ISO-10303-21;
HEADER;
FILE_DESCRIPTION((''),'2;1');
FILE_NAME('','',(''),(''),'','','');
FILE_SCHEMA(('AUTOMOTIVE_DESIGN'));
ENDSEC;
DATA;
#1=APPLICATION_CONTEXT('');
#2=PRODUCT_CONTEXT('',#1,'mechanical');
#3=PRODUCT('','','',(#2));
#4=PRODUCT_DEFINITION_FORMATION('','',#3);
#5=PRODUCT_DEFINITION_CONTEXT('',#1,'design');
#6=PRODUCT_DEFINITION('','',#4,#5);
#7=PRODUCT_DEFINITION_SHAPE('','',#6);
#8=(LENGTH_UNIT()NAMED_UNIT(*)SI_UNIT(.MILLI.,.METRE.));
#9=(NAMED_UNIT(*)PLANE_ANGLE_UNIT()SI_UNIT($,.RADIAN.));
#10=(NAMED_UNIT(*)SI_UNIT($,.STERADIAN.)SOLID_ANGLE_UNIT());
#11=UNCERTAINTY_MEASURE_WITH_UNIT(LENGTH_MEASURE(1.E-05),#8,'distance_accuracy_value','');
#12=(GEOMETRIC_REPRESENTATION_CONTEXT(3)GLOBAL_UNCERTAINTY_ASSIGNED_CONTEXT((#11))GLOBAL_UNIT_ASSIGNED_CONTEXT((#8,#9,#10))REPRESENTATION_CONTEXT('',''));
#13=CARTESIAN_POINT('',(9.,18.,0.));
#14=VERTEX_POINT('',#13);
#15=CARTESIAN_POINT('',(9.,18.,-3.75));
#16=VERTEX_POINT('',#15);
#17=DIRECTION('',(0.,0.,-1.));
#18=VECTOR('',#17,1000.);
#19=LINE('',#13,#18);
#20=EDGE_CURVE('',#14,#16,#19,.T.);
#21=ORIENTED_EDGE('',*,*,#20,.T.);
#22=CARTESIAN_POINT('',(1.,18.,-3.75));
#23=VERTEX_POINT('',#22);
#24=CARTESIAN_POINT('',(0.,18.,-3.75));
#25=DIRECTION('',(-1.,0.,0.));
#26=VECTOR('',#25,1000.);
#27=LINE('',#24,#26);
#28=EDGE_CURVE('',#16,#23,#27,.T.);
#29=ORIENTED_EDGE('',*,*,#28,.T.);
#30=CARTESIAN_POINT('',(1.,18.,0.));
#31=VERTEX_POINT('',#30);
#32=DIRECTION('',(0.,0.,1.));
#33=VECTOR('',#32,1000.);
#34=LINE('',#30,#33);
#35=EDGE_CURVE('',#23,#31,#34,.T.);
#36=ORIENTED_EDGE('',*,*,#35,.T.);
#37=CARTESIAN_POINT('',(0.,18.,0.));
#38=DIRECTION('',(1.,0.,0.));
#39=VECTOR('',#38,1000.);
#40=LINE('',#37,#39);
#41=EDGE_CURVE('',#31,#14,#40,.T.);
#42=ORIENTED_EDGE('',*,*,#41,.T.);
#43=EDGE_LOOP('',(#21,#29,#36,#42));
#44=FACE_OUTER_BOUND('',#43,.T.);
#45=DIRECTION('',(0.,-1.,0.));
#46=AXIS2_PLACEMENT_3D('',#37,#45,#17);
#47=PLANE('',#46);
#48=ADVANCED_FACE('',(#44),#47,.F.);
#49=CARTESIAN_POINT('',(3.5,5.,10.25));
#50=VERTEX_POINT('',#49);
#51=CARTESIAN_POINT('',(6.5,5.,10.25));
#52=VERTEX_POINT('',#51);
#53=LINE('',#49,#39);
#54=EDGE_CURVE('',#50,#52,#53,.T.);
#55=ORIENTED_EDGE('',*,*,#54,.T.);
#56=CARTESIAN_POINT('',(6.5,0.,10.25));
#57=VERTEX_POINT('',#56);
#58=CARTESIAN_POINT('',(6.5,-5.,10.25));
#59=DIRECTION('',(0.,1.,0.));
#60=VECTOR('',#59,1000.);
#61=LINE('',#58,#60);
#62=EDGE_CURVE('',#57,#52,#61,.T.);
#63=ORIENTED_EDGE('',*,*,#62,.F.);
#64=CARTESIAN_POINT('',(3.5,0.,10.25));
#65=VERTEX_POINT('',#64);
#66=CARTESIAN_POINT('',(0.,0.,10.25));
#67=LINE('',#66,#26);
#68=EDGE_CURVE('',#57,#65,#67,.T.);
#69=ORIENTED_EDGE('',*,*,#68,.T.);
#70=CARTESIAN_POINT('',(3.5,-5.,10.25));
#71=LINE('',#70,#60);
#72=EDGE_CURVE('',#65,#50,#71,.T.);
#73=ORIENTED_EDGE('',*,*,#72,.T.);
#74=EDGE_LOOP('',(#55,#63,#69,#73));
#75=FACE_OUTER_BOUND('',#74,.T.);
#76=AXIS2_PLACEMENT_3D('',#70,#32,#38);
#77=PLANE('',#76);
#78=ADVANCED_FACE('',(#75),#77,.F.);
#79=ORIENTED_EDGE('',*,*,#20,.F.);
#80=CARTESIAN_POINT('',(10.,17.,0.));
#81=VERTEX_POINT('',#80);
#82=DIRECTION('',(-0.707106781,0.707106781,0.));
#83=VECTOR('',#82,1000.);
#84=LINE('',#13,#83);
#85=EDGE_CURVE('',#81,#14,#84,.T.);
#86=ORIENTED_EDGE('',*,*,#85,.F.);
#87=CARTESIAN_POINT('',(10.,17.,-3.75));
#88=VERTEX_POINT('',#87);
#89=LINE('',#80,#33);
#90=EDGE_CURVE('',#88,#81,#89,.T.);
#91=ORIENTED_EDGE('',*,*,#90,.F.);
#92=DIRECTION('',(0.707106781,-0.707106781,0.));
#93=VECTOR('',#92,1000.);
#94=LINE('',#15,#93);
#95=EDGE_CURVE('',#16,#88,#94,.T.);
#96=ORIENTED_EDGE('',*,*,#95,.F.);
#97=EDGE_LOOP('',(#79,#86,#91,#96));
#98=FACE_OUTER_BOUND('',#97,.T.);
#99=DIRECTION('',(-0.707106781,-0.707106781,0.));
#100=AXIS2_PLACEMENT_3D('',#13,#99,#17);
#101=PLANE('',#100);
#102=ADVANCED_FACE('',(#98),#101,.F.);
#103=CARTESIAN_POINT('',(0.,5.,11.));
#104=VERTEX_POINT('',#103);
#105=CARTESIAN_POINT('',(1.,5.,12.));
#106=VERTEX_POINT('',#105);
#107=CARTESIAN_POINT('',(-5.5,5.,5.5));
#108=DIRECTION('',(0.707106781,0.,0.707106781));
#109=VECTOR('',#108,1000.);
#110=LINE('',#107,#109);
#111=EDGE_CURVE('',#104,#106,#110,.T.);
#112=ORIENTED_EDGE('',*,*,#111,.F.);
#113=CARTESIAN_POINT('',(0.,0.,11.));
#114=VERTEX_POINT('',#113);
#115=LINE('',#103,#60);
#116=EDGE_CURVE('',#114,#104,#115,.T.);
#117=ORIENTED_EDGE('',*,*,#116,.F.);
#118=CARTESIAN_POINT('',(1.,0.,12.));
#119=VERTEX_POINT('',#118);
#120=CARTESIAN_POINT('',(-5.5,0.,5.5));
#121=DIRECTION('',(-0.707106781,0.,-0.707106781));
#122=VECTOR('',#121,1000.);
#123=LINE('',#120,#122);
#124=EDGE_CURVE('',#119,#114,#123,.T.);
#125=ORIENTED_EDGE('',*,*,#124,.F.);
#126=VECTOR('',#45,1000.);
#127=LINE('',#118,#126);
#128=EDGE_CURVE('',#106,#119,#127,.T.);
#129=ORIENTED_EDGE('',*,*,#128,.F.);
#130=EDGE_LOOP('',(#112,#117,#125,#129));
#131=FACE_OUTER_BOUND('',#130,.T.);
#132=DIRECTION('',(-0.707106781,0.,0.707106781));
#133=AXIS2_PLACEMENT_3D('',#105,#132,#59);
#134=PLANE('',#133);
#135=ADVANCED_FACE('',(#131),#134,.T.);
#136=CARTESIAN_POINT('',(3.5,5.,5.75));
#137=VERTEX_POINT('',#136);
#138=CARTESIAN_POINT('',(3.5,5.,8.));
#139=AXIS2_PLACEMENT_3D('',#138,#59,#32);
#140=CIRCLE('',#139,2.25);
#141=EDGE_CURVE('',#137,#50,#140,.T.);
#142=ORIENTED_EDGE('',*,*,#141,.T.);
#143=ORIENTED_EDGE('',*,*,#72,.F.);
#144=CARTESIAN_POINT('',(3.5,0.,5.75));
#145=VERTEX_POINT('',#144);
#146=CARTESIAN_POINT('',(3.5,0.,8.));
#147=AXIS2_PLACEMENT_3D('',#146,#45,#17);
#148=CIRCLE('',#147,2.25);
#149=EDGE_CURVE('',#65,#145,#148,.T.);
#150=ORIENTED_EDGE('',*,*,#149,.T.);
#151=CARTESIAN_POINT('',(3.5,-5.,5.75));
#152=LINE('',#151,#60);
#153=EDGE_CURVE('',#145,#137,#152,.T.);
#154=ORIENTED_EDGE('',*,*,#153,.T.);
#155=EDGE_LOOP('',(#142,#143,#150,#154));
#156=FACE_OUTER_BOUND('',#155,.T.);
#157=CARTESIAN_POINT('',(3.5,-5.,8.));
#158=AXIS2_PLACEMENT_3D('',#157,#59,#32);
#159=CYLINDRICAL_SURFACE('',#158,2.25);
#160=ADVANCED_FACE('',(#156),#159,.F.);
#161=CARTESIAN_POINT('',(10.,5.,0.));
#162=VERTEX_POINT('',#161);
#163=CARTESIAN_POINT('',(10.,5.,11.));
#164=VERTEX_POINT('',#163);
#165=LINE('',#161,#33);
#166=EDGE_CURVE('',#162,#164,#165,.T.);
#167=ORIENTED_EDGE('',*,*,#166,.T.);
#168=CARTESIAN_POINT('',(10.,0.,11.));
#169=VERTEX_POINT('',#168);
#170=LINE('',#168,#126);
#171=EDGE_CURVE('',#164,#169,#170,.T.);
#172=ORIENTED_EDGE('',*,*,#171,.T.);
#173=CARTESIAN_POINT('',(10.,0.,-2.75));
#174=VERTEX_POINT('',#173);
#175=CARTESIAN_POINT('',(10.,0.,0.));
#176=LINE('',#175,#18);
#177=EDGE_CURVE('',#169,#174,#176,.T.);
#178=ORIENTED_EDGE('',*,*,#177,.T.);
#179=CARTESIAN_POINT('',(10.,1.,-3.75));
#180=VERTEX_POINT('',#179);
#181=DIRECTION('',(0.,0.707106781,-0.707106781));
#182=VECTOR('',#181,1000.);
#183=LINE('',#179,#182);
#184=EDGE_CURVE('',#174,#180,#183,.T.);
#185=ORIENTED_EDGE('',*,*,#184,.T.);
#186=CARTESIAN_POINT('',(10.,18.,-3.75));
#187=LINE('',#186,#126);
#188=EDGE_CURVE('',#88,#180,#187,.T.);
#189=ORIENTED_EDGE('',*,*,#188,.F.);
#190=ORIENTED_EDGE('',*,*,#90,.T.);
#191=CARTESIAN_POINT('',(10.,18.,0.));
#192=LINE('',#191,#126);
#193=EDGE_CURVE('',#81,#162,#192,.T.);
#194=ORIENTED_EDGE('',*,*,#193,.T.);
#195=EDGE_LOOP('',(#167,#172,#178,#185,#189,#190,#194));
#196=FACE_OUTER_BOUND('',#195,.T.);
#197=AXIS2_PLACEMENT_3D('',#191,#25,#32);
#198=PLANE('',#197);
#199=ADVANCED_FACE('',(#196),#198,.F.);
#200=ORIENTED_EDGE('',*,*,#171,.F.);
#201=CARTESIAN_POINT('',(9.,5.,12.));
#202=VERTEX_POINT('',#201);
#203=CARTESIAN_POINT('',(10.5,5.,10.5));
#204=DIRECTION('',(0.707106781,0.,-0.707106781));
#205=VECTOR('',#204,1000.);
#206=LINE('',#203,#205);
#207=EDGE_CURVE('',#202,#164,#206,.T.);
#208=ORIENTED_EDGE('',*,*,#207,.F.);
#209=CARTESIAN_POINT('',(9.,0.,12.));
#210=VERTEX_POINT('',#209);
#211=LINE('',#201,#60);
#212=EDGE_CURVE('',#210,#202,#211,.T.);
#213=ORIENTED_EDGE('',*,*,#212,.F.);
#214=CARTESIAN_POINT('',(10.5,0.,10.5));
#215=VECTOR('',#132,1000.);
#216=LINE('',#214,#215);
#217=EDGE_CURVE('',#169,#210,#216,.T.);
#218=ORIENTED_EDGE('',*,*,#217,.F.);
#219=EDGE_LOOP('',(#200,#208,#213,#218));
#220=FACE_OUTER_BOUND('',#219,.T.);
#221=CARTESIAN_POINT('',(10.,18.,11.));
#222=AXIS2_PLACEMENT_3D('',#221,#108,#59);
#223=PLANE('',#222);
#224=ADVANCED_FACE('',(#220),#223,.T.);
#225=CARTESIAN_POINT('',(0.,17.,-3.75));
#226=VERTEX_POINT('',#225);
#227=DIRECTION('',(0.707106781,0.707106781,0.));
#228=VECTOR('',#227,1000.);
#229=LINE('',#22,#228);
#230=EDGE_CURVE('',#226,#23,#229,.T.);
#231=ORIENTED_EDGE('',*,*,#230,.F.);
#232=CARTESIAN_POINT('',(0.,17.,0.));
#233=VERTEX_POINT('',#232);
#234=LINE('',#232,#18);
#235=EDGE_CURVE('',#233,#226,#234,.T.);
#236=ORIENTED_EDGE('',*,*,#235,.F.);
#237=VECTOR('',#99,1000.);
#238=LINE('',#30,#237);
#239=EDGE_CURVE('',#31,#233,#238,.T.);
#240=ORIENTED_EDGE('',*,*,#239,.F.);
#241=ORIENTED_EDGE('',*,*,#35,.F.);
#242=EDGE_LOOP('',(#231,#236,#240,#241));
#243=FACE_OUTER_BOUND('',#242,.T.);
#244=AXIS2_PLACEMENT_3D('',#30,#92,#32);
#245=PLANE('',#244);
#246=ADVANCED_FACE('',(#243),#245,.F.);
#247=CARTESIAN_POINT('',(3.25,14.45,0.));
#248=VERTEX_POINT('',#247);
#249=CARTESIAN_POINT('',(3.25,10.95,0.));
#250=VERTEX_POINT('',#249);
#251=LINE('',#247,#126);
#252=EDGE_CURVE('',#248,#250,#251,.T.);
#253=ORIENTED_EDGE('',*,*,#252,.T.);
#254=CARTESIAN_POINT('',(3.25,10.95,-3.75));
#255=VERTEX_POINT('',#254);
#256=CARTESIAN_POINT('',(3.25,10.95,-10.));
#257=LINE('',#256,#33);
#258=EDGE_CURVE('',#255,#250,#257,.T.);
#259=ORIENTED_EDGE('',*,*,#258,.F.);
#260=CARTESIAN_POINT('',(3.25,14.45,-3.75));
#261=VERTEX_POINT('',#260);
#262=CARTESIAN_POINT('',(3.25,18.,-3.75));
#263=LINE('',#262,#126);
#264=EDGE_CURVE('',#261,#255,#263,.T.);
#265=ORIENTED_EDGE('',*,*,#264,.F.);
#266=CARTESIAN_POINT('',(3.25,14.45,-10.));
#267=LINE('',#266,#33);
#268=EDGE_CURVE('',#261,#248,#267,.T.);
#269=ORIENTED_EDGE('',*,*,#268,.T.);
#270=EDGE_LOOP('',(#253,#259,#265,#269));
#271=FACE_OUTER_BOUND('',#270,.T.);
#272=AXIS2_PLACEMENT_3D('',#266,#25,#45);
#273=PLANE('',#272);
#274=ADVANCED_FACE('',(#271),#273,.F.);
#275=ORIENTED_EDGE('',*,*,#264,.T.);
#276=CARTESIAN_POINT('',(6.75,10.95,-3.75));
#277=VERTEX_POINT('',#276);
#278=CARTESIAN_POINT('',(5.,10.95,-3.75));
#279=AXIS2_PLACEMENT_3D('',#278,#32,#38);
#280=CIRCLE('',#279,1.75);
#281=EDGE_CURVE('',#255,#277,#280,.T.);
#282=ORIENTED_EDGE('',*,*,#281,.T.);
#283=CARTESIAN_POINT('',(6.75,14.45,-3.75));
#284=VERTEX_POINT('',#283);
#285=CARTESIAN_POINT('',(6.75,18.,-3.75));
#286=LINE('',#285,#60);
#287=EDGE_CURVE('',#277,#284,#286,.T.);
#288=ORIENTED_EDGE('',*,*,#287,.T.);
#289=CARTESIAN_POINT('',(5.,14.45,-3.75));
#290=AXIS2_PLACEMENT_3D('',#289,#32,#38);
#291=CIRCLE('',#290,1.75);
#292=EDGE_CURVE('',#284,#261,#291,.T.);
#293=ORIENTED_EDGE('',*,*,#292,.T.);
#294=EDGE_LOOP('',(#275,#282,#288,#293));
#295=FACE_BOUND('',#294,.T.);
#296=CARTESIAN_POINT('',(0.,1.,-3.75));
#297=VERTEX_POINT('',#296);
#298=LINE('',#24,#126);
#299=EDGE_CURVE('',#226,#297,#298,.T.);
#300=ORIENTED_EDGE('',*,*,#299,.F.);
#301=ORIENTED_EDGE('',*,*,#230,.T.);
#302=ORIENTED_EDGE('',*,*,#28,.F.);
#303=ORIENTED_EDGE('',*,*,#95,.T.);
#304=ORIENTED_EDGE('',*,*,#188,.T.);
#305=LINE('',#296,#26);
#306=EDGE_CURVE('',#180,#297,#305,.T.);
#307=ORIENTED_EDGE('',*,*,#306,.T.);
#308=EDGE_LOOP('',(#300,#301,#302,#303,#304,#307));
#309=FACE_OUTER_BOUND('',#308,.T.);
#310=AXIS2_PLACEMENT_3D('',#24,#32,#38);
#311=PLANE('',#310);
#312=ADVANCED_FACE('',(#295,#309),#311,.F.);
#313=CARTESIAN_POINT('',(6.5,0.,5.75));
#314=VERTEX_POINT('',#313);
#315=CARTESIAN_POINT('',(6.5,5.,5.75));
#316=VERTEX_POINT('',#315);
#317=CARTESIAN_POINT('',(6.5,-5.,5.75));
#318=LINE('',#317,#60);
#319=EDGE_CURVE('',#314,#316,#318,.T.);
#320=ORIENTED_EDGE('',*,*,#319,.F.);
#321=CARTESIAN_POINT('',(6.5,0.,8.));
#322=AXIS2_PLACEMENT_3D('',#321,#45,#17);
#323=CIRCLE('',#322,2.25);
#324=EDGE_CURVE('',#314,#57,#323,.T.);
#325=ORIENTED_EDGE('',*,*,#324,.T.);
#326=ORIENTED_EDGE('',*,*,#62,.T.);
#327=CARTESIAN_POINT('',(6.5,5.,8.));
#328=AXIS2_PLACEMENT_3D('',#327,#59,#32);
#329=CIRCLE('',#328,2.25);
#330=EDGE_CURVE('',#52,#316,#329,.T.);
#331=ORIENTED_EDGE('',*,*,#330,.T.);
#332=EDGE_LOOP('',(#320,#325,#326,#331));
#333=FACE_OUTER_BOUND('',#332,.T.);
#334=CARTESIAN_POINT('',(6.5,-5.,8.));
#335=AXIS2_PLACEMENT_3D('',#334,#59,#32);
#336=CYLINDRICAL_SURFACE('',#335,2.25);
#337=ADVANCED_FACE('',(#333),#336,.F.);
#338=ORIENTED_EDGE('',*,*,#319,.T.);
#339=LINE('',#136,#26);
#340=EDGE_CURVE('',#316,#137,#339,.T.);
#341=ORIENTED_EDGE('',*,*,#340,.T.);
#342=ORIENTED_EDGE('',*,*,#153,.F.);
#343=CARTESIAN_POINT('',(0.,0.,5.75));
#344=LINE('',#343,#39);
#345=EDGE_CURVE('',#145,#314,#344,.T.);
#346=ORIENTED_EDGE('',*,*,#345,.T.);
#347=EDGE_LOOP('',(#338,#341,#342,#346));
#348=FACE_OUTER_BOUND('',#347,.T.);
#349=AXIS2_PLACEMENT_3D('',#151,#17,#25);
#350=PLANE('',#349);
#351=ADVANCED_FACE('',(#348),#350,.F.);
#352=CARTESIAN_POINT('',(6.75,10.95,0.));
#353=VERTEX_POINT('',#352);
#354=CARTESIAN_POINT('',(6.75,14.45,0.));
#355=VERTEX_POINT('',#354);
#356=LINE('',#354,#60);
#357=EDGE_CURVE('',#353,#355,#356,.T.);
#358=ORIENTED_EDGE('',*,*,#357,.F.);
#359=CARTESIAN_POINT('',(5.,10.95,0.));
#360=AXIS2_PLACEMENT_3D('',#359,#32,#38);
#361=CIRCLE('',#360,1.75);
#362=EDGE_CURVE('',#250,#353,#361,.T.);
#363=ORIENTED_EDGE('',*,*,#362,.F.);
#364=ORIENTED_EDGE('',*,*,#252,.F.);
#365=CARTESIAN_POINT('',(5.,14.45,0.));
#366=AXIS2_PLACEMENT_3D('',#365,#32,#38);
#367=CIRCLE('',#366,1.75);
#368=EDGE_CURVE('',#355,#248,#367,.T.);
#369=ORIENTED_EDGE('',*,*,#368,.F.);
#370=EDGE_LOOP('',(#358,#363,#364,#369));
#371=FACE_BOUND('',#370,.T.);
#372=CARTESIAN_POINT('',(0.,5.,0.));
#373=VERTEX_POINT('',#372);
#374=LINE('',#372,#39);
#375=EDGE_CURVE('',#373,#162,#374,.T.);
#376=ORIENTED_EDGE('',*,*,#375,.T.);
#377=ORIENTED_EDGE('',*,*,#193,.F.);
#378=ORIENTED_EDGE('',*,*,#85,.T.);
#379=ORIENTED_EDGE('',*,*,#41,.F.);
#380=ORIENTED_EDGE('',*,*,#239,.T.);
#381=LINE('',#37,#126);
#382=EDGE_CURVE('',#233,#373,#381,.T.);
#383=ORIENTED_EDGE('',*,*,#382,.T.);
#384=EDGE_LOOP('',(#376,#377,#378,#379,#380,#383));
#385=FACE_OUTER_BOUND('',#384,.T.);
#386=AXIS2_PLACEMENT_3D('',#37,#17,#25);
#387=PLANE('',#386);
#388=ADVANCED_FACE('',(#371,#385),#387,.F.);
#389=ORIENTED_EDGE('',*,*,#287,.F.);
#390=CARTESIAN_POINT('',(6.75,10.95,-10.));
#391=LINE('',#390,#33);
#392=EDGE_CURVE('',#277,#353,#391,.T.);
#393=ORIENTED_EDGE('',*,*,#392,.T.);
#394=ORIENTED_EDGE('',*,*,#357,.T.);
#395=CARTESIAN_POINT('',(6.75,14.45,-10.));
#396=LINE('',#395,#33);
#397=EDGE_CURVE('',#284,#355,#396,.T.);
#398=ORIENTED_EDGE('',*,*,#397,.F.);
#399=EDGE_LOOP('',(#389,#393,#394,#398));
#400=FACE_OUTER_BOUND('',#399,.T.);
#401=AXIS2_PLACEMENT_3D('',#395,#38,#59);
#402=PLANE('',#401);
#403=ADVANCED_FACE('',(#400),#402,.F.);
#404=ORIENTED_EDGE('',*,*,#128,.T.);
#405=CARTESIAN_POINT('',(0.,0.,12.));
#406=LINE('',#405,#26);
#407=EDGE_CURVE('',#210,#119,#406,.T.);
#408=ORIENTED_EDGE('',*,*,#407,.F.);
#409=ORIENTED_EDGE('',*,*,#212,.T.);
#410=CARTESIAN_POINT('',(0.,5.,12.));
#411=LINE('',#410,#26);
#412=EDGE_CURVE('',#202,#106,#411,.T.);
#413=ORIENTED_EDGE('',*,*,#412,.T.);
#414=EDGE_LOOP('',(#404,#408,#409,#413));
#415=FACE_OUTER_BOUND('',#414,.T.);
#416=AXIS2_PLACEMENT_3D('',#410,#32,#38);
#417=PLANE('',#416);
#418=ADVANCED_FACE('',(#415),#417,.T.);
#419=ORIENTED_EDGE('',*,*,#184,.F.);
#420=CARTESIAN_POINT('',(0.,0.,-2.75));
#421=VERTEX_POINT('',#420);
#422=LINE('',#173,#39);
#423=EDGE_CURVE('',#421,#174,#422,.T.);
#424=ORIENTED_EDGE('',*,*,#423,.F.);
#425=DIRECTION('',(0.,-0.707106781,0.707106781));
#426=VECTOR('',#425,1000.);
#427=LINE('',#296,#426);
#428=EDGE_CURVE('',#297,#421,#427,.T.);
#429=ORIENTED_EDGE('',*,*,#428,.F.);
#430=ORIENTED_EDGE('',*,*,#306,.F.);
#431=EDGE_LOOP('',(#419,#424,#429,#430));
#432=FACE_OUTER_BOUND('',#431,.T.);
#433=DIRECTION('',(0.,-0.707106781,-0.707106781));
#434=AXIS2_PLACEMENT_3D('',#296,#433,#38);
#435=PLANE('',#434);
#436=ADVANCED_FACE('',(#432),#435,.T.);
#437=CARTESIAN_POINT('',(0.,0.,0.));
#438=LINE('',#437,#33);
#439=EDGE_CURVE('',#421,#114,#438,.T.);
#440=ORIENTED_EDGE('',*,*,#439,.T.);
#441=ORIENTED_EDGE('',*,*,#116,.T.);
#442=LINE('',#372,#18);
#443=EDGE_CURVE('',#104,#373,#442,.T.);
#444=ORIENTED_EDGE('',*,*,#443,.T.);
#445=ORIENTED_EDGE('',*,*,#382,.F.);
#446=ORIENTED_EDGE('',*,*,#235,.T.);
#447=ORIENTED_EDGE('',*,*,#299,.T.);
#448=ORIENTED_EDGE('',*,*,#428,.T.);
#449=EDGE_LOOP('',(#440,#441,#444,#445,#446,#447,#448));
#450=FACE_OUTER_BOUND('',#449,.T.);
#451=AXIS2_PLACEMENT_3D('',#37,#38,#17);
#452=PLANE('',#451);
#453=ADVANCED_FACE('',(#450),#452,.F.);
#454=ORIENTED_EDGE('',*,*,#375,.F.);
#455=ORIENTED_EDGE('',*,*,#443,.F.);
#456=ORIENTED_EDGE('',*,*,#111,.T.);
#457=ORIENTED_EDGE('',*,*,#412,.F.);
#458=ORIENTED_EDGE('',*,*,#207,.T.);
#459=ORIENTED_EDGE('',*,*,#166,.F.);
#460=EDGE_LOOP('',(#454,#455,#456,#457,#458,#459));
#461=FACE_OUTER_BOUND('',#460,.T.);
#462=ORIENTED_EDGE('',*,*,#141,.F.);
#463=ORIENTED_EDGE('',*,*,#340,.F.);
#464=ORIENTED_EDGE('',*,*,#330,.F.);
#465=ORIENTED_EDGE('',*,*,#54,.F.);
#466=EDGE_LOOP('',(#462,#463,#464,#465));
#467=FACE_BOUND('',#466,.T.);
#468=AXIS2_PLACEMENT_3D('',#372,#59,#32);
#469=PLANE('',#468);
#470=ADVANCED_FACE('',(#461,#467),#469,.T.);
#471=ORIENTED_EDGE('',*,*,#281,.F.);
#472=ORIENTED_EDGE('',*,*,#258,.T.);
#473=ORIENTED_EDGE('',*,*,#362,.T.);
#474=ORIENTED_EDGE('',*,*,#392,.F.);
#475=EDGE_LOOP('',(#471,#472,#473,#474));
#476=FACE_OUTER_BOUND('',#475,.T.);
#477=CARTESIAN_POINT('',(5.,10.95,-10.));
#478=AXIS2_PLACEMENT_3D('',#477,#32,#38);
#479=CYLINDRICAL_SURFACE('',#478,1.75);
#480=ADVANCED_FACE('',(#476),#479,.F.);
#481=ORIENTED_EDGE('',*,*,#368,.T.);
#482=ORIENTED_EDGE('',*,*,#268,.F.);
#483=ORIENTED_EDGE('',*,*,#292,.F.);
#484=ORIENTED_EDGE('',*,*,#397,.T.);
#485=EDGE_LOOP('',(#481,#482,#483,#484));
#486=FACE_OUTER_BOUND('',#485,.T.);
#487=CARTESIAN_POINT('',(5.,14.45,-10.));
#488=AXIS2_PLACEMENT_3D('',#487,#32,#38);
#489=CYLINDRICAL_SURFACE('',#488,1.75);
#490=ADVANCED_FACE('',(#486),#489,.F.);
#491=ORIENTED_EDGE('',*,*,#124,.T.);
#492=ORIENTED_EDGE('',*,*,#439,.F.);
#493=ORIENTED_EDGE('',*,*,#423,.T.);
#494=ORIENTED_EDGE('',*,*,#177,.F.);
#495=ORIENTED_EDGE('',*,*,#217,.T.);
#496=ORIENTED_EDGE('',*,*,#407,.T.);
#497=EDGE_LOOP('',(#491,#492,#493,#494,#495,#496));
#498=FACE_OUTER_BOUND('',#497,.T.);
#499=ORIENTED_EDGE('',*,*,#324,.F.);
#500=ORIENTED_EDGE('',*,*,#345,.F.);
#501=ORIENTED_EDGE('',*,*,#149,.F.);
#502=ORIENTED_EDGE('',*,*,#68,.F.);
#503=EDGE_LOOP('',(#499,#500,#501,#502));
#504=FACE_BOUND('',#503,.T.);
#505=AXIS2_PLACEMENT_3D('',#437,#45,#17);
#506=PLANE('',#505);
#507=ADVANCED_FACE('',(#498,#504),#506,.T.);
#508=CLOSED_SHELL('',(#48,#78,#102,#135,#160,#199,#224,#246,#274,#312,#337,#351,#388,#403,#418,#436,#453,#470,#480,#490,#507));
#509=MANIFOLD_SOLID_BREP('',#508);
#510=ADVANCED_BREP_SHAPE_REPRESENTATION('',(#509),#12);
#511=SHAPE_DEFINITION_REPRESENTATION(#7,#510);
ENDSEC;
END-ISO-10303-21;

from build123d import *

# Parameters (mm, degrees)
SKETCH1_W           = 10
SKETCH1_H           = 3.75
BOSS_EXTRUDE1_DEPTH = 18
SKETCH2_R           = 1.75
CUT_EXTRUDE1_DEPTH  = 20
SKETCH3_W           = 10
SKETCH3_H           = 12
BOSS_EXTRUDE2_DEPTH = 5
CUT_EXTRUDE2_DEPTH  = 10
CHAMFER1_SIZE       = 1
CUT_EXTRUDE3_DEPTH  = 10


with BuildPart() as part:
    # Sketch1 → Boss-Extrude1 (new body)
    with BuildSketch(Plane(origin=(0, 0, 0), x_dir=(1, 0, 0), z_dir=(0, 1, 0))):
        with Locations((5, 1.875)):
            Rectangle(SKETCH1_W, SKETCH1_H)
    extrude(amount=BOSS_EXTRUDE1_DEPTH)

    # Sketch2 → Cut-Extrude1 (cut)
    with BuildSketch(Plane.XY):
        with Locations((5, 12.7)):
            Circle(SKETCH2_R)
    extrude(amount=-CUT_EXTRUDE1_DEPTH, mode=Mode.SUBTRACT)

    # Sketch3 → Boss-Extrude2 (add)
    with BuildSketch(Plane.XZ):
        with Locations((5, 6)):
            Rectangle(SKETCH3_W, SKETCH3_H)
    extrude(amount=-BOSS_EXTRUDE2_DEPTH)

    # Sketch4 → Cut-Extrude2 (cut)
    with BuildSketch(Plane(origin=(0, 5, 0), x_dir=(1, 0, 0), z_dir=(0, 1, 0))):
        with BuildLine():
            Line((3.5, -10.25), (6.5, -10.25))
            ThreePointArc((6.5, -10.25), (8.75, -8), (6.5, -5.75))
            Line((6.5, -5.75), (3.5, -5.75))
            ThreePointArc((3.5, -5.75), (1.25, -8), (3.5, -10.25))
        make_face()
    extrude(amount=-CUT_EXTRUDE2_DEPTH, mode=Mode.SUBTRACT)

    # Chamfer1
    chamfer1_edges = [part.edges().sort_by_distance(p)[0] for p in [
        (10, 18, -1.875),
        (0, 2.5, 12),
        (10, 2.5, 12),
        (0, 18, -1.875),
        (5, 0, -3.75),
    ]]
    chamfer(chamfer1_edges, length=CHAMFER1_SIZE)

    # Sketch5 → Cut-Extrude3 (cut)
    with BuildSketch(Plane.XY):
        with BuildLine():
            Line((6.75, 14.45), (6.75, 10.95))
            ThreePointArc((6.75, 10.95), (5, 9.2), (3.25, 10.95))
            Line((3.25, 10.95), (3.25, 14.45))
            ThreePointArc((3.25, 14.45), (5, 16.2), (6.75, 14.45))
        make_face()
    extrude(amount=-CUT_EXTRUDE3_DEPTH, mode=Mode.SUBTRACT)


solid = part.part
